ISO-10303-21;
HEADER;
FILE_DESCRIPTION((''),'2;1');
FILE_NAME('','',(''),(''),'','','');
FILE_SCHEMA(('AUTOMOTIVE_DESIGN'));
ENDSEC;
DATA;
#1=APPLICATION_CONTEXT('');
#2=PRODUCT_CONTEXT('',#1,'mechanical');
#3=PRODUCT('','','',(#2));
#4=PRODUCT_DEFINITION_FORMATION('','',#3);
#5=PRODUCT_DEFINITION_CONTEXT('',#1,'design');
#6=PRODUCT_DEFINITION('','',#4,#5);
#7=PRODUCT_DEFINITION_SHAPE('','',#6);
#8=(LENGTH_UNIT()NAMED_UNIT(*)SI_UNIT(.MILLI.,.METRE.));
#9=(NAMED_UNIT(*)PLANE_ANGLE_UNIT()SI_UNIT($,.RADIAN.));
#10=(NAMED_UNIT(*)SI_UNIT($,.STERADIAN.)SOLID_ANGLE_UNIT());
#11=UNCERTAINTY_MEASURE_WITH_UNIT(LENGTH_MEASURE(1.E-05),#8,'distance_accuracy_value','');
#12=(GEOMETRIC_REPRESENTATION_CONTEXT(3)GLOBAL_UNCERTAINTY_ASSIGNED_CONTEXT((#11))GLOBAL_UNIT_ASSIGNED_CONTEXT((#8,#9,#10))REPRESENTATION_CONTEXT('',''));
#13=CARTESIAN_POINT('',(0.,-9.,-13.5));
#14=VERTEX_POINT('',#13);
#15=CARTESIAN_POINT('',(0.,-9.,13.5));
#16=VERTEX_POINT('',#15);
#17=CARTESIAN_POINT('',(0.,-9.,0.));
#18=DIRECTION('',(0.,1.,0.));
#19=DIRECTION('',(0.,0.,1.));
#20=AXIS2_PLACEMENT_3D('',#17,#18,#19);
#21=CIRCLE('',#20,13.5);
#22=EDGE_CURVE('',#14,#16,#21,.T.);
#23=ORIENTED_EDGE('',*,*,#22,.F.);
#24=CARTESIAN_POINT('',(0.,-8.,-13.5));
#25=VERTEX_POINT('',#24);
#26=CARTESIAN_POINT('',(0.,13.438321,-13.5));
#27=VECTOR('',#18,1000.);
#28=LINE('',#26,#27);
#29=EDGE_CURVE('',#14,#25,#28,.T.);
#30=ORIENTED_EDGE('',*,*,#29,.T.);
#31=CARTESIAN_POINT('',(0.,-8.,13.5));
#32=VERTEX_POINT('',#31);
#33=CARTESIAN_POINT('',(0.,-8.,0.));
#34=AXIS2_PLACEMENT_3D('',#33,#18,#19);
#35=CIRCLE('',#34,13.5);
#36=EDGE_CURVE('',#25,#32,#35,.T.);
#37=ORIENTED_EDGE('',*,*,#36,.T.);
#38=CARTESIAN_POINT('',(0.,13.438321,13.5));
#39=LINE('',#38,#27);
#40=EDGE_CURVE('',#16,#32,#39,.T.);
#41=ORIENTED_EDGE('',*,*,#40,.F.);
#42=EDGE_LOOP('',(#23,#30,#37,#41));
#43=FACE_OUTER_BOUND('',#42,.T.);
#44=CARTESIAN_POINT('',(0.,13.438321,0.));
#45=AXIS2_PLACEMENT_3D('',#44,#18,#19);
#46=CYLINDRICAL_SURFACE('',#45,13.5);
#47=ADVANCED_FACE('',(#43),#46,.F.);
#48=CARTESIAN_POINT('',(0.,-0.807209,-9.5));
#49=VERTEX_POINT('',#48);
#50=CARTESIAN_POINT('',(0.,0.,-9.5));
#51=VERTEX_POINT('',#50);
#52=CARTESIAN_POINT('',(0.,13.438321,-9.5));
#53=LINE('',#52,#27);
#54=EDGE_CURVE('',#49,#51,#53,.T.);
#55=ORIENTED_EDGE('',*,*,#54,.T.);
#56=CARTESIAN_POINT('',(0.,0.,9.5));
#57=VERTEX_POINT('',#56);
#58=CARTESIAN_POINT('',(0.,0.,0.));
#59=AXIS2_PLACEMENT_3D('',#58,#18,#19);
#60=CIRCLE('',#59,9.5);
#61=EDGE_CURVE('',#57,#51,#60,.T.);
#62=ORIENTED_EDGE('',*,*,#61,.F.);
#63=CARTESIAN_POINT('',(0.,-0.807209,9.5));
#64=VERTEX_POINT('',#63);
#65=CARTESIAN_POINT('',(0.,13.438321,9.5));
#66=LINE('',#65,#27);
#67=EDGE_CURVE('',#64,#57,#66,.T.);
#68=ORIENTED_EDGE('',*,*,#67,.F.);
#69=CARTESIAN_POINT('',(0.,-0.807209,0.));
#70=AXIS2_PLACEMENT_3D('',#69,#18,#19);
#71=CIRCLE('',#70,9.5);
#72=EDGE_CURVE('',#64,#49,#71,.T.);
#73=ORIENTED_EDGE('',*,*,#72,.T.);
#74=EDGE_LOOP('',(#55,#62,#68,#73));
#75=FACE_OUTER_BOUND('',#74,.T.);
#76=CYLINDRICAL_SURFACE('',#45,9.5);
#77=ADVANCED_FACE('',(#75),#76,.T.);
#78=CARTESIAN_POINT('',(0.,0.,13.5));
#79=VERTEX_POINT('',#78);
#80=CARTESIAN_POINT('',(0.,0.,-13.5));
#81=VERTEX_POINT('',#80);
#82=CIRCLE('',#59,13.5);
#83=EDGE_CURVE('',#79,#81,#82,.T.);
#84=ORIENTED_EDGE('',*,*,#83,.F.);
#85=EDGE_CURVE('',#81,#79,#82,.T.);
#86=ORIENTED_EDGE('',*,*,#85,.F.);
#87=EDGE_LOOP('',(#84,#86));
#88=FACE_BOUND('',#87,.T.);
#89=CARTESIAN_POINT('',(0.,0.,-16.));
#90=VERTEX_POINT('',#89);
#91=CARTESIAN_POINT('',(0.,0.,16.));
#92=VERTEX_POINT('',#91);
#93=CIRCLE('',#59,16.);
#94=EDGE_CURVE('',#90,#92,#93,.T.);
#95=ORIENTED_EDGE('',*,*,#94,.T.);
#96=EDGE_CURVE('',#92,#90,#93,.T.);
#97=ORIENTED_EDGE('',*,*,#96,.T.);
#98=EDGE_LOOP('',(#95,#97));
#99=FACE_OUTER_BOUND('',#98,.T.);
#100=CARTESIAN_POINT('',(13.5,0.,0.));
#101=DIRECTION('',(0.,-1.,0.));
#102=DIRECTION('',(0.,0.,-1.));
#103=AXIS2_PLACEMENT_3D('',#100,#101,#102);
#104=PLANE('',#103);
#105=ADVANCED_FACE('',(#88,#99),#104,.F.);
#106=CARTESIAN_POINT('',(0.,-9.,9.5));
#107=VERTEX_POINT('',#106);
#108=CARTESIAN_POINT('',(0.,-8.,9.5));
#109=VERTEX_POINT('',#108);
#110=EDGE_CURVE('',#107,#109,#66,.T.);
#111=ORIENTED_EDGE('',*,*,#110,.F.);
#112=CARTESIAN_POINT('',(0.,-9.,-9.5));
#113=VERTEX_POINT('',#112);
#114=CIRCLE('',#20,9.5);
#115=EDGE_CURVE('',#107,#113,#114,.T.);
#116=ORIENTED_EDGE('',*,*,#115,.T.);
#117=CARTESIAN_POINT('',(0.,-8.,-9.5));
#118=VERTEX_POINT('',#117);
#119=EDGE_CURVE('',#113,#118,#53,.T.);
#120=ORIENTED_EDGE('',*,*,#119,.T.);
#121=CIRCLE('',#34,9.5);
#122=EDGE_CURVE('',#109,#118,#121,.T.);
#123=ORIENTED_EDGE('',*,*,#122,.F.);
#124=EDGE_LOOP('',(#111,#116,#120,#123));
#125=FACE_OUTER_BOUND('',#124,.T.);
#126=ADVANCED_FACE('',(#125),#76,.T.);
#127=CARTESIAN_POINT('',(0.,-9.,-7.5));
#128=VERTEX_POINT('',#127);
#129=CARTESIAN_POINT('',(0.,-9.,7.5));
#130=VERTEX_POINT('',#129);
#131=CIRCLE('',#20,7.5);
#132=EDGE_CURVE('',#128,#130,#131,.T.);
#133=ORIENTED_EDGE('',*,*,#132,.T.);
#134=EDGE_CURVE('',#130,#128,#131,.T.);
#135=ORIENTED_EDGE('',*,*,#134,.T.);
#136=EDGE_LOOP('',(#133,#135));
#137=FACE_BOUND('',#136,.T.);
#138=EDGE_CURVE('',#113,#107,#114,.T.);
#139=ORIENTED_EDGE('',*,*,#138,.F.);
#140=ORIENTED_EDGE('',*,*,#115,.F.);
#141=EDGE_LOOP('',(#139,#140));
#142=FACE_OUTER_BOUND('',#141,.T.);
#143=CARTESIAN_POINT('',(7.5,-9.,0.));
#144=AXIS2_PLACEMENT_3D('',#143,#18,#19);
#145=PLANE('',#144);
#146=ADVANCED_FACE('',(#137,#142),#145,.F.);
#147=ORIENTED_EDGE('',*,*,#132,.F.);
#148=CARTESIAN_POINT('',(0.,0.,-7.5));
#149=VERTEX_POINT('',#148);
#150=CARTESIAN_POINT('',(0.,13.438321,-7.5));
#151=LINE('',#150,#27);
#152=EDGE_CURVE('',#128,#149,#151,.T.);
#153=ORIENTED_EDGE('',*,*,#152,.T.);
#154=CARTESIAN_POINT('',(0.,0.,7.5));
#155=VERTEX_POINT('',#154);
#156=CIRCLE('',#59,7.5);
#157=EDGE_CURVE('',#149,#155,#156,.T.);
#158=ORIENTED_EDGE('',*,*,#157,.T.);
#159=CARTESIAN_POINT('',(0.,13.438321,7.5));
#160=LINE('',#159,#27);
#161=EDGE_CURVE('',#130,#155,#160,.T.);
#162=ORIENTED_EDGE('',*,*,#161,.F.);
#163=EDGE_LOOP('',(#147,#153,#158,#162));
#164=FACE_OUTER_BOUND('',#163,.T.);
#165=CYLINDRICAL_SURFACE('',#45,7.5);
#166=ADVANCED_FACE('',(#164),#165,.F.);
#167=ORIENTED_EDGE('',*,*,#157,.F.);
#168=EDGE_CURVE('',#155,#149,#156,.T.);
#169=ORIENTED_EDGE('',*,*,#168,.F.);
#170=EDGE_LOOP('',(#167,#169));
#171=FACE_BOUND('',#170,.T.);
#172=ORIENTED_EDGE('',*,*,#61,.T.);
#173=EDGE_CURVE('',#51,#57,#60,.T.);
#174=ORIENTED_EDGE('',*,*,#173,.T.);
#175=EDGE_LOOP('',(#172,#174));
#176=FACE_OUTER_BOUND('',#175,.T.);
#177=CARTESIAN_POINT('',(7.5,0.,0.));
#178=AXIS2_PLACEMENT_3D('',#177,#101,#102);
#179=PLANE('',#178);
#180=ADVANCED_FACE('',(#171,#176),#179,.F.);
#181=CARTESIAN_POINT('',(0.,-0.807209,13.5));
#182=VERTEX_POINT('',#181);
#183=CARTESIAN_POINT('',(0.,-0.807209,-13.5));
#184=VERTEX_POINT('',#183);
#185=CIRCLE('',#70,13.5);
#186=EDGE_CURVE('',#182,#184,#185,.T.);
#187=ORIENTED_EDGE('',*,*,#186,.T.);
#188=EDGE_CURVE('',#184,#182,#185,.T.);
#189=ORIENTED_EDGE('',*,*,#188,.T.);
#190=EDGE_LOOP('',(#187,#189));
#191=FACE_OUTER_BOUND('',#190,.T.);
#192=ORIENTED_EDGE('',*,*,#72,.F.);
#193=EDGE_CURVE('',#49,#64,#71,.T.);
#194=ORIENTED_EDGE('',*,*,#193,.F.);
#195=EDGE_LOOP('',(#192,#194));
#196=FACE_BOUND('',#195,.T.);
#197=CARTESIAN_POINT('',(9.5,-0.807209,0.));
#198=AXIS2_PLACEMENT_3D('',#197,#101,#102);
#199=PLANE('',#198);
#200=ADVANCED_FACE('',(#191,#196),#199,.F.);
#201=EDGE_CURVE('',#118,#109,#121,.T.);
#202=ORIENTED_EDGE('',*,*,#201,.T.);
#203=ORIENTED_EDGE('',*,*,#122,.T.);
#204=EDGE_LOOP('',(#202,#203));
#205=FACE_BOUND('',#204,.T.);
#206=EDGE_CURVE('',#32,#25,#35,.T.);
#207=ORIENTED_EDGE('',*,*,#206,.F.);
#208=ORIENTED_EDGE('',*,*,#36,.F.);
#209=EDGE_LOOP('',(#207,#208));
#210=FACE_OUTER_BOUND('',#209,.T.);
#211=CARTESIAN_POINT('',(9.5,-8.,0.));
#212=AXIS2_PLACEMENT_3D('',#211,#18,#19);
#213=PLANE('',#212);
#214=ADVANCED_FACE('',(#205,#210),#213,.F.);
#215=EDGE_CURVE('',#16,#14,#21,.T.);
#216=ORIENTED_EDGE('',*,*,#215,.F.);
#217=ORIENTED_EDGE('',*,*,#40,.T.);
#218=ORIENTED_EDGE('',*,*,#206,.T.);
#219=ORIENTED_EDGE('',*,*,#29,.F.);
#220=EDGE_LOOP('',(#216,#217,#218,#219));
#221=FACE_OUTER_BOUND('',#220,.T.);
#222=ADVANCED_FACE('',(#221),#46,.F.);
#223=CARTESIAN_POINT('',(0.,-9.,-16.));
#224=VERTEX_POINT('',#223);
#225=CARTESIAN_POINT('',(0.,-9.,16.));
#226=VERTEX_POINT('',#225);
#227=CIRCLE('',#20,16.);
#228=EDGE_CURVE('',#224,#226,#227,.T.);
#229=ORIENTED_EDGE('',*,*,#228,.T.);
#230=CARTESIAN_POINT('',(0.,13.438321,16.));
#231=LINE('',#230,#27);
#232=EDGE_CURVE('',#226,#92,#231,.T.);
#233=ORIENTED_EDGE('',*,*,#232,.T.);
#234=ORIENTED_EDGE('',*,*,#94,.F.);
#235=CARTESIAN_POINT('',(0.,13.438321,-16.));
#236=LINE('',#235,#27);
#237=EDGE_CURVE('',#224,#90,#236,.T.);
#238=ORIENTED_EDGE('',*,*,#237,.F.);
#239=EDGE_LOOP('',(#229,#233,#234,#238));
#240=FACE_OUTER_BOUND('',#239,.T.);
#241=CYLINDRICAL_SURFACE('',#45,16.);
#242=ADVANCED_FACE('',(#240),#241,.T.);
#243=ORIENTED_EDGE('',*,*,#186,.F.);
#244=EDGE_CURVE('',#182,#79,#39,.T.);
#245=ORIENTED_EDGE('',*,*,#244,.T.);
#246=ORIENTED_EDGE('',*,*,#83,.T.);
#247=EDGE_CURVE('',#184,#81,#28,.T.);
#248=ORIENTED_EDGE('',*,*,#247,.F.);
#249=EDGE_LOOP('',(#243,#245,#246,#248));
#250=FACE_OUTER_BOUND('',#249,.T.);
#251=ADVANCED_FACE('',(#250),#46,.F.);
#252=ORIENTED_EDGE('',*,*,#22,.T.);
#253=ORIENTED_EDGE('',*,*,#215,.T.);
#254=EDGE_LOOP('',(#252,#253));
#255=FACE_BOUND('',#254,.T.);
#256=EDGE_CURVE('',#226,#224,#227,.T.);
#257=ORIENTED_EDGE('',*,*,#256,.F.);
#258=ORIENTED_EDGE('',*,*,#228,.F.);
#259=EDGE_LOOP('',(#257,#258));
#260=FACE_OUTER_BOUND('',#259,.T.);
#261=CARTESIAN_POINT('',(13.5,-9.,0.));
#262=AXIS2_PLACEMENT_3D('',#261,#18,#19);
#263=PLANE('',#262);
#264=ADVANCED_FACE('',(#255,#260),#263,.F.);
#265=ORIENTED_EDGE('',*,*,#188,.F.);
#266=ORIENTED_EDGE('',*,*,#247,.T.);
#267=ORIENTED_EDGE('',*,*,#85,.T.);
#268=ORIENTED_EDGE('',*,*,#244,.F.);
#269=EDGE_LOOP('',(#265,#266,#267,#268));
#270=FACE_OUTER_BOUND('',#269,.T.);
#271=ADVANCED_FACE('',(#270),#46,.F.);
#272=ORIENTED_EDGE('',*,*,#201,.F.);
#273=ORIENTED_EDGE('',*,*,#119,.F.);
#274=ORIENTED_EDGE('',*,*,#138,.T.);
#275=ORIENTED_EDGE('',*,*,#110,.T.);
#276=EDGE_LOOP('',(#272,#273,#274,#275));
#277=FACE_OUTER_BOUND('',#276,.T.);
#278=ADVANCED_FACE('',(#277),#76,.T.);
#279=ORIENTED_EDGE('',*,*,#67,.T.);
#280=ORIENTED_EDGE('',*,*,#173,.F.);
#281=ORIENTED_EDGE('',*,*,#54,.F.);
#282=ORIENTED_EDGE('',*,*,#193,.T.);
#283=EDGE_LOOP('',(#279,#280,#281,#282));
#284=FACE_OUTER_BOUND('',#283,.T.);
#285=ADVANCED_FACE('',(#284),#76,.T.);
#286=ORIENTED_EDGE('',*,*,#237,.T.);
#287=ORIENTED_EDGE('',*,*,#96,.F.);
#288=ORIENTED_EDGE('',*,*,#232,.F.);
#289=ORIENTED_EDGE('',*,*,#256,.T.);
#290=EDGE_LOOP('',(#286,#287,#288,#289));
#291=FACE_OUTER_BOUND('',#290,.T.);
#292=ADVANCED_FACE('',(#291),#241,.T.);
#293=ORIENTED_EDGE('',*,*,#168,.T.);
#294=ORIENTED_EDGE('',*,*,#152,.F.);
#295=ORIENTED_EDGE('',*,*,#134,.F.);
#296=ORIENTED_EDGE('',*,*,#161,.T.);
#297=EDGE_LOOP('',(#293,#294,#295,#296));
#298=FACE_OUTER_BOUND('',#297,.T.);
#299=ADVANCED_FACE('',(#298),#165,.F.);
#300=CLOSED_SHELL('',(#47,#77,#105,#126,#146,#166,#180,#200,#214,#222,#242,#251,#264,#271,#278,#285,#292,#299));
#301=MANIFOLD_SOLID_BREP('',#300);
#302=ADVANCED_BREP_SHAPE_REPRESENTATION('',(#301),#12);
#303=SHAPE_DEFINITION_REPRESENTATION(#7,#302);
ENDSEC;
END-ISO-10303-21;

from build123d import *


with BuildPart() as part:
    # 草图1 → 旋转1 (revolve)
    with BuildSketch(Plane.XY, mode=Mode.PRIVATE) as revolve_1_sk:
        Polygon((7.5, 0), (7.5, -9), (9.5, -9), (9.5, -8), (13.5, -8), (13.5, -9), (16, -9), (16, 0), (13.5, 0), (13.5, -0.807209449), (9.5, -0.807209449), (9.5, 0), align=None)
    revolve(revolve_1_sk.sketch.rotate(Axis((0, 13.438321286, 0), (0, -1, 0)), 90), axis=Axis((0, 13.438321286, 0), (0, -1, 0)))


solid = part.part
